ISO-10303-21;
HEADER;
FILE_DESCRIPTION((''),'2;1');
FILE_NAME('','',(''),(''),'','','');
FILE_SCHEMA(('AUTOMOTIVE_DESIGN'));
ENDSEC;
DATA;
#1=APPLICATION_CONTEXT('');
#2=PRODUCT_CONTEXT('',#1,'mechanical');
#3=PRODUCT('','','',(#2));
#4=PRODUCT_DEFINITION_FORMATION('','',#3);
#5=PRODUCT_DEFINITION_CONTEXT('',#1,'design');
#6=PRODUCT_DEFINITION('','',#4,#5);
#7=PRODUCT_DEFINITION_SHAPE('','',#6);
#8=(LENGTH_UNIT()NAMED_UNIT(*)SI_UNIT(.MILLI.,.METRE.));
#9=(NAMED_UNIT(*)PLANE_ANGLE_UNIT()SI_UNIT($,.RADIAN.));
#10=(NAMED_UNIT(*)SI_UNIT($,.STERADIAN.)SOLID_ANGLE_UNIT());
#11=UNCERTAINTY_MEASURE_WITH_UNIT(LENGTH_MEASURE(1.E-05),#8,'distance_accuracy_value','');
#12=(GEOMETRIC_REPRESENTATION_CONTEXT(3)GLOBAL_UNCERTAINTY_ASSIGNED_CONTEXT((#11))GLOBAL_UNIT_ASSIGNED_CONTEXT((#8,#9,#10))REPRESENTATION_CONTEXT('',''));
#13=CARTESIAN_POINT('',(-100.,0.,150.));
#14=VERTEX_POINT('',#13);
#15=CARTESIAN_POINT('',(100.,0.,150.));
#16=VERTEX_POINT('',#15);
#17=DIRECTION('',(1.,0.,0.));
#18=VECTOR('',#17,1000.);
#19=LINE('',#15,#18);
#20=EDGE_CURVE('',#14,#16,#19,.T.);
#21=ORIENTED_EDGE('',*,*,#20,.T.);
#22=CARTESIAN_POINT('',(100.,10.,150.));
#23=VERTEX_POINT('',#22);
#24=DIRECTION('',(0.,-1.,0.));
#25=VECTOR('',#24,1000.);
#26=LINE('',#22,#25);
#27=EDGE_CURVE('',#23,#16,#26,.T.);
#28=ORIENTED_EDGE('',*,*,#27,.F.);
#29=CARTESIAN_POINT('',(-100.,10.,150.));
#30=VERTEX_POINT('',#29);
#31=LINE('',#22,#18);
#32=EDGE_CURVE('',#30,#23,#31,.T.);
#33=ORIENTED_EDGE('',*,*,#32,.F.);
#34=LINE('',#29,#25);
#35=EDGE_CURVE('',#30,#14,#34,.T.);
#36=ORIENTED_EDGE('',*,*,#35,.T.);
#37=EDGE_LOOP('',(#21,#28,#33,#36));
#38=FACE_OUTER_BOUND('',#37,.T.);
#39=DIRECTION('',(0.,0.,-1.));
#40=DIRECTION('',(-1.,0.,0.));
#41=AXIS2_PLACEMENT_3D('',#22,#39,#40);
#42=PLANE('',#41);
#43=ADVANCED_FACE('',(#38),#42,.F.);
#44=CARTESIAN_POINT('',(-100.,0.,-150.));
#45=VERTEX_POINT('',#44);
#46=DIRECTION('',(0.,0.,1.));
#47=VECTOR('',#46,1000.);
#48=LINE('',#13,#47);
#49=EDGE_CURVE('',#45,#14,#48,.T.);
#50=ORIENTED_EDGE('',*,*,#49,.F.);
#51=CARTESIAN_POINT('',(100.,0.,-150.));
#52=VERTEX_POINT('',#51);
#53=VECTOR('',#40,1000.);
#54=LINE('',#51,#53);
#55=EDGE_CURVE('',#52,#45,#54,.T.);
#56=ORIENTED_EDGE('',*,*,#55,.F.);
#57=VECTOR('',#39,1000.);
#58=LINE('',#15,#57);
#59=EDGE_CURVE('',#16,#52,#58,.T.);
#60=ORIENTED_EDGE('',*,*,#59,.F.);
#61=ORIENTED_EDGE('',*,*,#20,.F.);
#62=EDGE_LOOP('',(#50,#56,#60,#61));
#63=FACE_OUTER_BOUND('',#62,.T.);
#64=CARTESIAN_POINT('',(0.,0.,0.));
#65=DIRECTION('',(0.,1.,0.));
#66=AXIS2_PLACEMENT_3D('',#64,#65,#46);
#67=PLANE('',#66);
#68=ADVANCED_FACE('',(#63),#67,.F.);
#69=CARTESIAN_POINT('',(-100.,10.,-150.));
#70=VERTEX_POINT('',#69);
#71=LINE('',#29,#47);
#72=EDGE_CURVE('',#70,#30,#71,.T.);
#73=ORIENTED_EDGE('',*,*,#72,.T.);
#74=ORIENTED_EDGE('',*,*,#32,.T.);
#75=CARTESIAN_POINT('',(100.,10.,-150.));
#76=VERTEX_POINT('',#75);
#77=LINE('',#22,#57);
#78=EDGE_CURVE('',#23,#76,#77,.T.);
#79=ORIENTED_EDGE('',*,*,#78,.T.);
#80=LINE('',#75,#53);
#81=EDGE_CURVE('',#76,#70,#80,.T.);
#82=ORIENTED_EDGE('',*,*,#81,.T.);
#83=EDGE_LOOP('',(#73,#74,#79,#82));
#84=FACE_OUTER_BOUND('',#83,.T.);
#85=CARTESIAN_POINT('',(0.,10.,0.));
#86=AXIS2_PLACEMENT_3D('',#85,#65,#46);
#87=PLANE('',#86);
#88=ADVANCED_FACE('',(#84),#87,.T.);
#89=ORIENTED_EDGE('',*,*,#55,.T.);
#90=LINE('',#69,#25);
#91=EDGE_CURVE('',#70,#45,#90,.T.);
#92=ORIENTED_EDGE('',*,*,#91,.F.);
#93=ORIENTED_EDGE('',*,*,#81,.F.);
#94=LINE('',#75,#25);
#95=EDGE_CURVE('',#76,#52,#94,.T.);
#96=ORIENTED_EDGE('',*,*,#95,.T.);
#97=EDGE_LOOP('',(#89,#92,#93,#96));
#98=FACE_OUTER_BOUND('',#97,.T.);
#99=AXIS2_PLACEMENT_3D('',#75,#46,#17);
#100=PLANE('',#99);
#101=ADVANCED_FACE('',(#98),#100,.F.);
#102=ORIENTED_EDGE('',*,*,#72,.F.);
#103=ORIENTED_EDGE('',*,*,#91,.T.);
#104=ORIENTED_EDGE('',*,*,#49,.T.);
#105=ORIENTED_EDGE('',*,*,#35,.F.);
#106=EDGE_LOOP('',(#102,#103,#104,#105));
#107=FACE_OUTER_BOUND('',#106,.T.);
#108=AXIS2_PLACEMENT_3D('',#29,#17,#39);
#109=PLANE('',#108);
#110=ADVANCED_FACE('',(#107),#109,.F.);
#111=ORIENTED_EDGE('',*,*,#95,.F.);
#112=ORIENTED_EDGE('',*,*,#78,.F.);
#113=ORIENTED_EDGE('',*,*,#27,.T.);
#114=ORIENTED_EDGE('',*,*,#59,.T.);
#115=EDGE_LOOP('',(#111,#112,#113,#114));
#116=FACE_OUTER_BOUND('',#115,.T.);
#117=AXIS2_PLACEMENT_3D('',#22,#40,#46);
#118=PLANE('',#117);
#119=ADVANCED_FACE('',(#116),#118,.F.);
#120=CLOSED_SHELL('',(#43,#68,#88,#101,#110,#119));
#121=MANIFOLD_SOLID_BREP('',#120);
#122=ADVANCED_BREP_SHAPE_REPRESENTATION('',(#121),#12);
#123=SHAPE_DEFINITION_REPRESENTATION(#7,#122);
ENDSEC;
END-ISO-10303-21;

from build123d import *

# Parameters (mm, degrees)
SKETCH2_W           = 200
SKETCH2_H           = 300
BOSS_EXTRUDE1_DEPTH = 10


with BuildPart() as part:
    # Sketch2 → Boss-Extrude1 (new body)
    with BuildSketch(Plane(origin=(0, 0, 0), x_dir=(1, 0, 0), z_dir=(0, 1, 0))):
        Rectangle(SKETCH2_W, SKETCH2_H)
    extrude(amount=BOSS_EXTRUDE1_DEPTH)


solid = part.part
